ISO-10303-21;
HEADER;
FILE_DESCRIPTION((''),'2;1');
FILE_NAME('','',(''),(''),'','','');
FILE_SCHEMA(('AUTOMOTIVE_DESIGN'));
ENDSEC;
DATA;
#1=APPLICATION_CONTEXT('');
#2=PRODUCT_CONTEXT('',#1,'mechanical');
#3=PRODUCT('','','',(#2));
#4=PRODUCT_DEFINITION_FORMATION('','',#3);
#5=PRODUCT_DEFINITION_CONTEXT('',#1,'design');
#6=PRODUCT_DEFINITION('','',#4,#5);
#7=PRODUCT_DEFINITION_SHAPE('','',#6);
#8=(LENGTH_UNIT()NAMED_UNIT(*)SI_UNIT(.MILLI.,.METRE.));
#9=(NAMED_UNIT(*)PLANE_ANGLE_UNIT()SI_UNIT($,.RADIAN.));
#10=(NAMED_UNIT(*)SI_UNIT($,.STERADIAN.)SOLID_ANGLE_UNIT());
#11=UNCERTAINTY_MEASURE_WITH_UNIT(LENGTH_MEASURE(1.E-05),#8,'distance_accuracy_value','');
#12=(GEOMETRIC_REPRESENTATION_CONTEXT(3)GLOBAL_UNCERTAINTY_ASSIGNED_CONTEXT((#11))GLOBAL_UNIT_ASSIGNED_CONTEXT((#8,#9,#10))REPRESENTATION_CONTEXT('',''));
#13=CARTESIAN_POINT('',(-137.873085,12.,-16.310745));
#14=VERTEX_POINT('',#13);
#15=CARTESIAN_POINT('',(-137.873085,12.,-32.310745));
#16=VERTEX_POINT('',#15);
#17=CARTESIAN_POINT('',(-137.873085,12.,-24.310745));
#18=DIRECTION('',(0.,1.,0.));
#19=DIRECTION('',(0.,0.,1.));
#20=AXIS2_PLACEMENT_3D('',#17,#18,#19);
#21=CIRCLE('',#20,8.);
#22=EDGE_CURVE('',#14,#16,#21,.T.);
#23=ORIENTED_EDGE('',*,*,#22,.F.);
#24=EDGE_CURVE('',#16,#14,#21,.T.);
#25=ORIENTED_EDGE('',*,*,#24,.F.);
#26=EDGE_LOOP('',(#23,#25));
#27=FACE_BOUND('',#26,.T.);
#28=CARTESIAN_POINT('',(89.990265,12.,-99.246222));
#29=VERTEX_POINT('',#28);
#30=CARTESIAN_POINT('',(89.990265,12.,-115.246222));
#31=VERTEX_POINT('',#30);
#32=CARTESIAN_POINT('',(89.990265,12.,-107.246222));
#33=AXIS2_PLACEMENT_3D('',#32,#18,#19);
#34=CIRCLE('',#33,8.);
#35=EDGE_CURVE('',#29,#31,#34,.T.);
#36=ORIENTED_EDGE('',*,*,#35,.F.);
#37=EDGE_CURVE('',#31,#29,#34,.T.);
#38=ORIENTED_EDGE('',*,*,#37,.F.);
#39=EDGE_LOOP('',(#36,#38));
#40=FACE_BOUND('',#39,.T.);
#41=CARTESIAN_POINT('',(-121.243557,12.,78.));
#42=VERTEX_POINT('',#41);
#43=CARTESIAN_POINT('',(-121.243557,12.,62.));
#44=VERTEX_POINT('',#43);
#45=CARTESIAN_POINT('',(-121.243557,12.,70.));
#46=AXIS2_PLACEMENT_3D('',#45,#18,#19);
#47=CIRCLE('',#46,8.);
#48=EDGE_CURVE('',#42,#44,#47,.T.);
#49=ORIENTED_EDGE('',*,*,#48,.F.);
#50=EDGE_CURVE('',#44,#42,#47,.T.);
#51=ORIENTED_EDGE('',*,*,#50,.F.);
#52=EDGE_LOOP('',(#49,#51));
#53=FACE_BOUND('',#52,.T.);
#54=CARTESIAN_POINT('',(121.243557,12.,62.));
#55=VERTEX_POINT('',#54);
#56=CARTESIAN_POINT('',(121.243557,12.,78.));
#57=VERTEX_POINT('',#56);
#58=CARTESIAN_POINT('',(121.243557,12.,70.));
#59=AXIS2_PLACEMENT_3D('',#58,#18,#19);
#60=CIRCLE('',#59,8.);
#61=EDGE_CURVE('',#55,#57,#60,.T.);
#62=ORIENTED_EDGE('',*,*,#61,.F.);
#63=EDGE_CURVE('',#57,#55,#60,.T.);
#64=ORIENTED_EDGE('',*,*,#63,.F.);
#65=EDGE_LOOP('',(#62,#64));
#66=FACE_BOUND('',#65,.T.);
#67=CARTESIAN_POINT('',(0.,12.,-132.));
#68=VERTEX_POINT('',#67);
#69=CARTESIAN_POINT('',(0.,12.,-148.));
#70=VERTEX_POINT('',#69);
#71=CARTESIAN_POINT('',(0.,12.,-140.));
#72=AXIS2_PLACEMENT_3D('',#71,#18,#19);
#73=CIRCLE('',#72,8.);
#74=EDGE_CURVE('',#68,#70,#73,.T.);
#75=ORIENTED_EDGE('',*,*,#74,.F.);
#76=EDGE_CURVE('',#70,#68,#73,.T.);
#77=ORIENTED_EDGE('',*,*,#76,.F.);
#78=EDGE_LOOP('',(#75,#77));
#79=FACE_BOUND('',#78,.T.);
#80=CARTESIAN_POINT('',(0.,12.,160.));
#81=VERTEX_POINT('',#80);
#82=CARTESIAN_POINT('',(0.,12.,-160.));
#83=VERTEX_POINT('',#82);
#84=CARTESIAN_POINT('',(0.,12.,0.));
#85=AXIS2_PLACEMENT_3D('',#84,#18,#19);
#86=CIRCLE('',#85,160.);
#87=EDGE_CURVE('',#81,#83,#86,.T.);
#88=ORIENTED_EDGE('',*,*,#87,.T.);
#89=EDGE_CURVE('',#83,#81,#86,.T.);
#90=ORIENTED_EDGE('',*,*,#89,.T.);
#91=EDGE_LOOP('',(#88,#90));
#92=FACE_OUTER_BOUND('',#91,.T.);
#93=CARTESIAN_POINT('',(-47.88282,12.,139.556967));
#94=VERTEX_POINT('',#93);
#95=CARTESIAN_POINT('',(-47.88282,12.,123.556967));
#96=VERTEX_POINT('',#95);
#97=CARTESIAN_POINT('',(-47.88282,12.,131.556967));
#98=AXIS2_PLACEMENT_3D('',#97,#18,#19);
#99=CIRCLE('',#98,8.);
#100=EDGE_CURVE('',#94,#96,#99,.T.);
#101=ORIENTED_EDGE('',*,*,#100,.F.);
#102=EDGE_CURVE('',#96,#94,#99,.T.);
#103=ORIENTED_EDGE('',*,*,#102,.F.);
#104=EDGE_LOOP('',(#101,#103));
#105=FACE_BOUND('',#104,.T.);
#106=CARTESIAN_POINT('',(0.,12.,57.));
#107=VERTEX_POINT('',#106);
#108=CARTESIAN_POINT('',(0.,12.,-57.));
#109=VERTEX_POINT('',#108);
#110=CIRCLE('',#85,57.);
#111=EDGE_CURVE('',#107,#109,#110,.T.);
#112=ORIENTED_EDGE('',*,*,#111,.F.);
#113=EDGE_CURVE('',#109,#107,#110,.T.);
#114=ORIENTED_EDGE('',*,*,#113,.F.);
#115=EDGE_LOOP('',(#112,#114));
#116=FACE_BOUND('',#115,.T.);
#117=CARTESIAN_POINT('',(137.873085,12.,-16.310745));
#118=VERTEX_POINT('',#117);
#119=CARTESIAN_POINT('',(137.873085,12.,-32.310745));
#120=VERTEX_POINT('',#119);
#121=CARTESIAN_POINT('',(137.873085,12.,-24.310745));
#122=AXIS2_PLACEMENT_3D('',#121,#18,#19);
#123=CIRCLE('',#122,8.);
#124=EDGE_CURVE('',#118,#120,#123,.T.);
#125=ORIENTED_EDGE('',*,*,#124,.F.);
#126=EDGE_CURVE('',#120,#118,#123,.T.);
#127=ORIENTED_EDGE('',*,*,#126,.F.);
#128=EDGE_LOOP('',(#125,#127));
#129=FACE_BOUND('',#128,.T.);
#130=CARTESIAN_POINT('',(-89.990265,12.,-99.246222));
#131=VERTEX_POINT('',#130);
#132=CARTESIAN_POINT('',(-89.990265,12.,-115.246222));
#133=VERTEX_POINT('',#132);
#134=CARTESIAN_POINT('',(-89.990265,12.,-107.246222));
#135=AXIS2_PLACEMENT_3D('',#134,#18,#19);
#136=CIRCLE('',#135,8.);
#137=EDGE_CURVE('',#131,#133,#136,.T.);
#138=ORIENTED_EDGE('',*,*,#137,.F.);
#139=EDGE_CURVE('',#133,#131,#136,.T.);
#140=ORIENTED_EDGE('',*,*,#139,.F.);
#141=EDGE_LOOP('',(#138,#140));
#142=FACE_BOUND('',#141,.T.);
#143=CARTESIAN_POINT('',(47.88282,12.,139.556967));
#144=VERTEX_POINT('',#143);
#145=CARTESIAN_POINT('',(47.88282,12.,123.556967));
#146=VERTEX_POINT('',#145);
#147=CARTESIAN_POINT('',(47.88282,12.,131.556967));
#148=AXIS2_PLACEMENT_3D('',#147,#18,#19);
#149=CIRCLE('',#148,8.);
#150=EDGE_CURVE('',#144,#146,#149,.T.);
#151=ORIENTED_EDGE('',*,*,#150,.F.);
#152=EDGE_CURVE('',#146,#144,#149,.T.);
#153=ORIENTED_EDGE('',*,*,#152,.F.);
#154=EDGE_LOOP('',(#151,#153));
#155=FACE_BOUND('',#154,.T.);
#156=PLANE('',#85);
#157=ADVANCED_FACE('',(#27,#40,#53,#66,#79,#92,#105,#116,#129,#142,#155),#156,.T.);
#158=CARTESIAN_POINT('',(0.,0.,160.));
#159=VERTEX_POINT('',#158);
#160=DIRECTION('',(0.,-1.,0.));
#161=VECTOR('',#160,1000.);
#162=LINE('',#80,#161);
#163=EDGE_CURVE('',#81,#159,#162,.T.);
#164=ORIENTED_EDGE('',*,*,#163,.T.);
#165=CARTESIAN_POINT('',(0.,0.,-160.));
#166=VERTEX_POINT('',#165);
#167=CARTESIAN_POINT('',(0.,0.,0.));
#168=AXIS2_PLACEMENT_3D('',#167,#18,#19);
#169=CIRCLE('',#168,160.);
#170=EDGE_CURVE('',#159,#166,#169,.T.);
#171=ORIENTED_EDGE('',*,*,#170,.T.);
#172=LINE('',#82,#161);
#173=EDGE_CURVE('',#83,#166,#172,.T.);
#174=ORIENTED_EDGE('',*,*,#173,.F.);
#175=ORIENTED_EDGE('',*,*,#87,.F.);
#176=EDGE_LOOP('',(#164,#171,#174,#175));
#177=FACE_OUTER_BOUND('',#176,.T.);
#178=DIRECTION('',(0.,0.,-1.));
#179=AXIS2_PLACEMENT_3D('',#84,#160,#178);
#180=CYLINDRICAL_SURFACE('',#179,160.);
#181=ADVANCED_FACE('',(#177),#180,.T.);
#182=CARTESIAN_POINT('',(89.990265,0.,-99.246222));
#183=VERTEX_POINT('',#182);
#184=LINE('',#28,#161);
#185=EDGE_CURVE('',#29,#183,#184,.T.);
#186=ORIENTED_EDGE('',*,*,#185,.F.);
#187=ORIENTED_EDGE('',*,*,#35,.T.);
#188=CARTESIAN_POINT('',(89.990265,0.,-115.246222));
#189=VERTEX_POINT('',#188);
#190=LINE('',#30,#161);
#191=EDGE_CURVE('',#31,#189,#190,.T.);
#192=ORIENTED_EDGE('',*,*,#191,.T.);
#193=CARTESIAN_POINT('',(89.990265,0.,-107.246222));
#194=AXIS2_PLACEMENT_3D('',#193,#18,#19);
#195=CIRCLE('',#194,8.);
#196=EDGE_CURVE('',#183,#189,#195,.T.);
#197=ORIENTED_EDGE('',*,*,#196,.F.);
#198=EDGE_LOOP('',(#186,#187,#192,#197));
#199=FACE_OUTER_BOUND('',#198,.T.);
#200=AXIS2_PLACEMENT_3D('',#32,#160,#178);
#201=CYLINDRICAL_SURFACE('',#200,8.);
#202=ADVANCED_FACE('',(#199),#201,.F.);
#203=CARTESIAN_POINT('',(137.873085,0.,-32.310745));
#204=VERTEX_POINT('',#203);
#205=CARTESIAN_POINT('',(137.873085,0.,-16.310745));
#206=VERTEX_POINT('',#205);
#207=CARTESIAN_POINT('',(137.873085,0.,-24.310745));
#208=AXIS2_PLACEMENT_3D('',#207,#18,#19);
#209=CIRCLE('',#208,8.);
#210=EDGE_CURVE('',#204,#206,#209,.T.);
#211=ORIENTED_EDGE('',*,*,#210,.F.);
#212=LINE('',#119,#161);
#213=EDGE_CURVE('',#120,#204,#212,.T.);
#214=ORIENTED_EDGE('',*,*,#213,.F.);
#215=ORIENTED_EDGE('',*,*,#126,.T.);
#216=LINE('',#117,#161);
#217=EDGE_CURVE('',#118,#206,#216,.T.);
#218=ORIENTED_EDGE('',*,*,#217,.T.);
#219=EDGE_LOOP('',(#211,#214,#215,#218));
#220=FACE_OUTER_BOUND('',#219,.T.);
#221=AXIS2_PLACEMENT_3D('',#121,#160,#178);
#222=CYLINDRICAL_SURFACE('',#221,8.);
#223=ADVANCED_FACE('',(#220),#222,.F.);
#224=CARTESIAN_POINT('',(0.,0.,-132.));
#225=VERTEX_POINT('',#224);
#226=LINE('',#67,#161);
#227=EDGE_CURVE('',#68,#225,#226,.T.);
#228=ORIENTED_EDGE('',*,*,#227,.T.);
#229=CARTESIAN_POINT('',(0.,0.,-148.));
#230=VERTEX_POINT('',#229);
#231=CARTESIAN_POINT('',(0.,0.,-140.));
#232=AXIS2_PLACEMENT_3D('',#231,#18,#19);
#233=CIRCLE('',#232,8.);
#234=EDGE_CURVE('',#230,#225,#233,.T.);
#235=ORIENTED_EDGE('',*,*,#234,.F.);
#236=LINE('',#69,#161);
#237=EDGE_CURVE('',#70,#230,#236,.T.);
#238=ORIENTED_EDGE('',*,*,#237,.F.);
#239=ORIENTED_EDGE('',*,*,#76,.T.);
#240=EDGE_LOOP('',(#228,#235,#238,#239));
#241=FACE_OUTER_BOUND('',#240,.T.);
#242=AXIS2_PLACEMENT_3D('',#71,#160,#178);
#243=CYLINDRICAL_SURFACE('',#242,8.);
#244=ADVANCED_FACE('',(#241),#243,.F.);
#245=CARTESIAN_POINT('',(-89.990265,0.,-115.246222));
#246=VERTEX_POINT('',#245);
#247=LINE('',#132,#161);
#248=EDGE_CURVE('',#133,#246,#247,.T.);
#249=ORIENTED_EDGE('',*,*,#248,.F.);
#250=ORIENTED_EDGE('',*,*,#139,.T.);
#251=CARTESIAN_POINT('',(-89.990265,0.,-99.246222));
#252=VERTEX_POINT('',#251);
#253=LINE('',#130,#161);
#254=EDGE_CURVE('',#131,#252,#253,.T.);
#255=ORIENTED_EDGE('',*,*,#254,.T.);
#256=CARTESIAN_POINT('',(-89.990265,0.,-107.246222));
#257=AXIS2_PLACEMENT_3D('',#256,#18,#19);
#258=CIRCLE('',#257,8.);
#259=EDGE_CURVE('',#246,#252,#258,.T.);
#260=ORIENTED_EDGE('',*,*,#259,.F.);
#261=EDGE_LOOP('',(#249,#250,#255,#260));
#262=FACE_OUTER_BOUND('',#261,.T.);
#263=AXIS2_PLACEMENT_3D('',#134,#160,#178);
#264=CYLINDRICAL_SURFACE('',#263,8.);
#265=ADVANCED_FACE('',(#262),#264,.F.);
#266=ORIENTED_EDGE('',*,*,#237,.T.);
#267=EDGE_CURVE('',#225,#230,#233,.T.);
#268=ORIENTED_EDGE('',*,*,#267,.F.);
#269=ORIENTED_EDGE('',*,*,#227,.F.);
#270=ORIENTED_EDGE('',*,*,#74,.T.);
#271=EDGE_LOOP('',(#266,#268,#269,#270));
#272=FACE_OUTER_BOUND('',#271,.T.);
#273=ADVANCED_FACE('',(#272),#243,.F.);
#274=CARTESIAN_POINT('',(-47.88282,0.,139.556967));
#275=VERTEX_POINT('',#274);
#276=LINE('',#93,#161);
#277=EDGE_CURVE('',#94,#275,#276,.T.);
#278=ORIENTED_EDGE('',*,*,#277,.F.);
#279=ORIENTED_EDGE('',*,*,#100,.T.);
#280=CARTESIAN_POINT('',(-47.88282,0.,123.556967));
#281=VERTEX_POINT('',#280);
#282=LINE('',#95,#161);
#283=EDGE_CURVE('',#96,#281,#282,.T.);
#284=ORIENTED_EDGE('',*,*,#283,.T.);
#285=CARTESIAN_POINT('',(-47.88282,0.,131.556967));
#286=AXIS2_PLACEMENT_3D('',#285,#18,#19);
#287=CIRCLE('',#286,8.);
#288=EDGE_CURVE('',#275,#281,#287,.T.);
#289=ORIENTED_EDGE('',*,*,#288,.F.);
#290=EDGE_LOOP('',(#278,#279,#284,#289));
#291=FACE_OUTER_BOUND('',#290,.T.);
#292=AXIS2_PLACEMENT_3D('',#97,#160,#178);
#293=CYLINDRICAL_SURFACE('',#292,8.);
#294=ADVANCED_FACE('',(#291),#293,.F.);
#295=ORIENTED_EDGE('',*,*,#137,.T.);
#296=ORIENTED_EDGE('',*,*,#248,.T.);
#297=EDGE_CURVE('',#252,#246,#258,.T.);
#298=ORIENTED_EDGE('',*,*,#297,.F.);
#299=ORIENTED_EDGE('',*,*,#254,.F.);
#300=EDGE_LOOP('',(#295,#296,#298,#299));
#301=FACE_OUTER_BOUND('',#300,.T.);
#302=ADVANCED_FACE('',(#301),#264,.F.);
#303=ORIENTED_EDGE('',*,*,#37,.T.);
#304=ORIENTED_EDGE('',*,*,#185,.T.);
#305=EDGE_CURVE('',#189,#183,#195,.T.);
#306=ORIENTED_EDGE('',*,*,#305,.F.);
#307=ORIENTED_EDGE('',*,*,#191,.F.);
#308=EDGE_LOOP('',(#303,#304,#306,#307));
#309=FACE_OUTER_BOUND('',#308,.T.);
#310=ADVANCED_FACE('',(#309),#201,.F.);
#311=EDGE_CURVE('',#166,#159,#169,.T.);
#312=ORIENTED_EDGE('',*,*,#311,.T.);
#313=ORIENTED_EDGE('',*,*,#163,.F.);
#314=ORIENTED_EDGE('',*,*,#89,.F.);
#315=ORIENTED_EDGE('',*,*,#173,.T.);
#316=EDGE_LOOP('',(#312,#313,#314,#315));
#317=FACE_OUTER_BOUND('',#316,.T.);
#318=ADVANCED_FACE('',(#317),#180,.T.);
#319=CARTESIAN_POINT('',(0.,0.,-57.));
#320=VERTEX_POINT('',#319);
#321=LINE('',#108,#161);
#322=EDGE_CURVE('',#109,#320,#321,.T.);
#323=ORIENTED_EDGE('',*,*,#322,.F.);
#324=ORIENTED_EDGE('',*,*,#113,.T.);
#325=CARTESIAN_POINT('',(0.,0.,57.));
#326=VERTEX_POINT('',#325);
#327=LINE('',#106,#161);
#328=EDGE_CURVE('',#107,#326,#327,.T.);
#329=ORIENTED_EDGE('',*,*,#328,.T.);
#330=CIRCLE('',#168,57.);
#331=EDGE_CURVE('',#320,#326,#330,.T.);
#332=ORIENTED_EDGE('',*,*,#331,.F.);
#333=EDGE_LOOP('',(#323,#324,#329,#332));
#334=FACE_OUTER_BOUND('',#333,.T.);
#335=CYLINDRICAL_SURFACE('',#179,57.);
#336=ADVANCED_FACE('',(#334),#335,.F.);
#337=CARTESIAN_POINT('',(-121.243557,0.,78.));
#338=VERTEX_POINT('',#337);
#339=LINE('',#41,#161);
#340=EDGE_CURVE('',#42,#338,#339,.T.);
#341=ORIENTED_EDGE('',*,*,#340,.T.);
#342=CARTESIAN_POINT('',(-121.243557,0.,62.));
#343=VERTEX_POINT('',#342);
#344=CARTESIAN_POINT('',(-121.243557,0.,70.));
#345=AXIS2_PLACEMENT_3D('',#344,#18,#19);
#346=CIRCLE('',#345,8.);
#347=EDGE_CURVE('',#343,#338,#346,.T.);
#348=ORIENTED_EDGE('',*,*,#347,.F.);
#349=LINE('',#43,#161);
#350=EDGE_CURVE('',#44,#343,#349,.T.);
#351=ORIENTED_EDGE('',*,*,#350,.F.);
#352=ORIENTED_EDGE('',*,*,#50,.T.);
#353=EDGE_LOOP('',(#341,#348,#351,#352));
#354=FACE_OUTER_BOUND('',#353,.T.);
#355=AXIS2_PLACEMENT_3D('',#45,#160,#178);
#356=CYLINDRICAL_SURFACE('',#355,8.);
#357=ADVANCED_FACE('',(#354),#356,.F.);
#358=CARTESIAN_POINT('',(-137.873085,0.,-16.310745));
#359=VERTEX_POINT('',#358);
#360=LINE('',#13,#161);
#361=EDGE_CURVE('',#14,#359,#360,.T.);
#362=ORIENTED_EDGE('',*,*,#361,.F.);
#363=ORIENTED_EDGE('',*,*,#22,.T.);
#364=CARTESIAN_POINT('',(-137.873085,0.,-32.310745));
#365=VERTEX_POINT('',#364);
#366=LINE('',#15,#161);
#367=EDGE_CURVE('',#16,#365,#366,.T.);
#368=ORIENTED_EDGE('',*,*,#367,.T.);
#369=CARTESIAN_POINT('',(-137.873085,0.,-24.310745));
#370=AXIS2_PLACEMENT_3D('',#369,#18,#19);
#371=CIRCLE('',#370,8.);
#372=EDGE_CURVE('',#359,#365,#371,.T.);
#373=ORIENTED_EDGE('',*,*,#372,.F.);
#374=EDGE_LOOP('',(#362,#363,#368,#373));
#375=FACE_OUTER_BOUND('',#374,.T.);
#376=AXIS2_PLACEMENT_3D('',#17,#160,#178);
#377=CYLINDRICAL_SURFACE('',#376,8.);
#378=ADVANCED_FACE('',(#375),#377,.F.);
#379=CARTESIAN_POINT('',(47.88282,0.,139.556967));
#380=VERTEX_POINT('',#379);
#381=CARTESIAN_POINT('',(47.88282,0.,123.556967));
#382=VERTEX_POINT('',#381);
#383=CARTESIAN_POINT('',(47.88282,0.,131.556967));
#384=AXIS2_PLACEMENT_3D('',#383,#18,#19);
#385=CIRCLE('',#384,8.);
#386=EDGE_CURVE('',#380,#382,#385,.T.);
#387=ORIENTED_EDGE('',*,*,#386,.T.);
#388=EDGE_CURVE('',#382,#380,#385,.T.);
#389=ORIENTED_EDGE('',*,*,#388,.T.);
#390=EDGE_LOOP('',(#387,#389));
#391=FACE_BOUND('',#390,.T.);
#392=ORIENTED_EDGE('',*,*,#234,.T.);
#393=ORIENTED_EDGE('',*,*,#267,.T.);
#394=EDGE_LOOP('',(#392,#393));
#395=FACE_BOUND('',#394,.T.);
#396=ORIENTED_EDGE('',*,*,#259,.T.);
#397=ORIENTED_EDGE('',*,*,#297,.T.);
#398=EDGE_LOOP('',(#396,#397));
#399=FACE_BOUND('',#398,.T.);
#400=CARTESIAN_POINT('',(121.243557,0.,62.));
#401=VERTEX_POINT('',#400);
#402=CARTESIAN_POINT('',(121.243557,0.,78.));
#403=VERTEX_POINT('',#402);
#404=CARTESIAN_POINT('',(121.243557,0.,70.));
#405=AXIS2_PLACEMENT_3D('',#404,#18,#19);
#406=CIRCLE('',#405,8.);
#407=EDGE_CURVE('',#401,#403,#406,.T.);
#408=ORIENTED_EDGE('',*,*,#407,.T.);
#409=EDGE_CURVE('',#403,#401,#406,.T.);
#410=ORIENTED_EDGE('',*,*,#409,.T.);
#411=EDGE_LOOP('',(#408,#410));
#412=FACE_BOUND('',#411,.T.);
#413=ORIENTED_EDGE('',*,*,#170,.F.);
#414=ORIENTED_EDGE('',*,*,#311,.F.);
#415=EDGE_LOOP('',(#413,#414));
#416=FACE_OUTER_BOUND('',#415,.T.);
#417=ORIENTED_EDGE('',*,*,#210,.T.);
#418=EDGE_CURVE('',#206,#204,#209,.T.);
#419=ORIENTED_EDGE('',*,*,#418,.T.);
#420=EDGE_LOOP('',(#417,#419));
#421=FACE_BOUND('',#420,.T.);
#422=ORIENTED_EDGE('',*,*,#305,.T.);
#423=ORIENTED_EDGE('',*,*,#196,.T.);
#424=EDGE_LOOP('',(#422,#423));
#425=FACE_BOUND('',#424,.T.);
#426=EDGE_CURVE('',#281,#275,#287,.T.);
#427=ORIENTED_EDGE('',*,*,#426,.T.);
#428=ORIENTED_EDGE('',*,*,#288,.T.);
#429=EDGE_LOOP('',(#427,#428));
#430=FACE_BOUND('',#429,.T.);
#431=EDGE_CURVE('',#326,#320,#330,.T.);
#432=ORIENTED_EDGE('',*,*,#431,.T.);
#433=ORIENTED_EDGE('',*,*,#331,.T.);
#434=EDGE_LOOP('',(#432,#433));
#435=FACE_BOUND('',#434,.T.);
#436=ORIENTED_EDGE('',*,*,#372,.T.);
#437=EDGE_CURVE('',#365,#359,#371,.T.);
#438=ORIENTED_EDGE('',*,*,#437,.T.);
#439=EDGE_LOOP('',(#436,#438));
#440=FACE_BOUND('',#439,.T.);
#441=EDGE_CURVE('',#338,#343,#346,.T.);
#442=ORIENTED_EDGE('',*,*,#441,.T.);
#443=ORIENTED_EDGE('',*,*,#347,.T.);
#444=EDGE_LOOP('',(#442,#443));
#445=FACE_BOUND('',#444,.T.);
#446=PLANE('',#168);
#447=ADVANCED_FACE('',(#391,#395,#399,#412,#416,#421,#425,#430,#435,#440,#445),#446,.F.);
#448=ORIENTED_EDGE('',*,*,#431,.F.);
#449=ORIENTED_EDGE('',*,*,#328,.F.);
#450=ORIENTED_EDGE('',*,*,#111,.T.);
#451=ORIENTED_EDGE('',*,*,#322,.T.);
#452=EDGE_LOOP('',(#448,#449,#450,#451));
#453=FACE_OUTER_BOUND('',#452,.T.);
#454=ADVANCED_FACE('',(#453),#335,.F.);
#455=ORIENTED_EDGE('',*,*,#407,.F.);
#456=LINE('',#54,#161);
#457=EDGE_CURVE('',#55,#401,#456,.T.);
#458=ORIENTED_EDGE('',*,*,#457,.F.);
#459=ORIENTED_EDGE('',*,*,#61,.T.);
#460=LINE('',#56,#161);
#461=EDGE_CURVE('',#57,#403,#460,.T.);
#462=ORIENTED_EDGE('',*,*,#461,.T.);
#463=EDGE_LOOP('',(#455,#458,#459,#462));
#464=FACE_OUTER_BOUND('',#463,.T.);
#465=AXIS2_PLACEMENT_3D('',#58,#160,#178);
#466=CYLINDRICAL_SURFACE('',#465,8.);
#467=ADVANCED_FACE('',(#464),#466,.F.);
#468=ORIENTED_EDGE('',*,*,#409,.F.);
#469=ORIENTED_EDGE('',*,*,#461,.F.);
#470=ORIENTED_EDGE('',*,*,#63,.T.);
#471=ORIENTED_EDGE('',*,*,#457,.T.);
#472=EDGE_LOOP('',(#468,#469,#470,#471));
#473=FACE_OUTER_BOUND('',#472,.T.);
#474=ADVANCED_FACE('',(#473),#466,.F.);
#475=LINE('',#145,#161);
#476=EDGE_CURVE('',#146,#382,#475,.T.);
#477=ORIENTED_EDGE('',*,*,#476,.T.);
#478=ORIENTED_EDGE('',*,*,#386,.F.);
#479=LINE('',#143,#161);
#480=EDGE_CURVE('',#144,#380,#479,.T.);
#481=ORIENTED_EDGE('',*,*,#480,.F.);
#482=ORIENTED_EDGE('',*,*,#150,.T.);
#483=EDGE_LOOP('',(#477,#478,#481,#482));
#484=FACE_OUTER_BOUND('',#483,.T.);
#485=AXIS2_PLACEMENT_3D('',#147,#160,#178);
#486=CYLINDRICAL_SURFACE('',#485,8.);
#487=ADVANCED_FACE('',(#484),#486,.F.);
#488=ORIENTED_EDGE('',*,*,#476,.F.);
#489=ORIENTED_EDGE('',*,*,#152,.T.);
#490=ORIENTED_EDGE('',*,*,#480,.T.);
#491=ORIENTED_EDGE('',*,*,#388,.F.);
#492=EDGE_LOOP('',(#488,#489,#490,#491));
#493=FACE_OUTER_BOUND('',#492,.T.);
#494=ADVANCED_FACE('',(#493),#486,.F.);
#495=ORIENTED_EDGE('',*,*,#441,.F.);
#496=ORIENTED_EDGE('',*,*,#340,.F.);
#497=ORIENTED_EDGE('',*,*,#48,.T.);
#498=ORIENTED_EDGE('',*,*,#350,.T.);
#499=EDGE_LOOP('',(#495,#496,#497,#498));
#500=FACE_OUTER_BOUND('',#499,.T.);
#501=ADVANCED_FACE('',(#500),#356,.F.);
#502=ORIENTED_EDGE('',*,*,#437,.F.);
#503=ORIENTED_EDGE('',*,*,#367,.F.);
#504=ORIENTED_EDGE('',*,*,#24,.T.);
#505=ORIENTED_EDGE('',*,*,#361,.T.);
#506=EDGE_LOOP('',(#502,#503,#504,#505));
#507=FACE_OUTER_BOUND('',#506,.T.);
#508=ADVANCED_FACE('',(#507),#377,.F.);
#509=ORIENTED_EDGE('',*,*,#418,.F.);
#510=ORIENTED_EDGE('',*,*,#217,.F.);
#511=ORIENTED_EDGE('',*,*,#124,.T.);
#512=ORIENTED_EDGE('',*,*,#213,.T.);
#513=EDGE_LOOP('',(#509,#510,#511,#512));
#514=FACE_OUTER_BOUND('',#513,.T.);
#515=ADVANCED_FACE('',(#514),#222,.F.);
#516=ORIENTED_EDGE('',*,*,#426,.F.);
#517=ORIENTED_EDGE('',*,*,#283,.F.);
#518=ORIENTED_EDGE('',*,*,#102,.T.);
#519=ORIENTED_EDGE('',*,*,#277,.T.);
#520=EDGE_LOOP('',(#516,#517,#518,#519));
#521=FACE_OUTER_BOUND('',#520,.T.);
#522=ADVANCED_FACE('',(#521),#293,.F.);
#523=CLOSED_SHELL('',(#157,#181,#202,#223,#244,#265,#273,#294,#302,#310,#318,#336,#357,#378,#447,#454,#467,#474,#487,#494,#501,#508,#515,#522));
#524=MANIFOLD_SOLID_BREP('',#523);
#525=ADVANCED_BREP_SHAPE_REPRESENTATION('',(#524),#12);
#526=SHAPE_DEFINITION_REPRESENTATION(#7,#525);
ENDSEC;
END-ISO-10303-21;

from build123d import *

# Parameters (mm, degrees)
SKETCH1_R           = 160
SKETCH1_R_2         = 57
SKETCH1_R_3         = 8
BOSS_EXTRUDE1_DEPTH = 12


with BuildPart() as part:
    # Sketch1 → Boss-Extrude1 (new body)
    with BuildSketch(Plane(origin=(0, 0, 0), x_dir=(1, 0, 0), z_dir=(0, 1, 0))):
        with Locations(Location((0, 0, 0), (0, 0, 270))):
            Circle(SKETCH1_R)
        with Locations(Location((0, 0, 0), (0, 0, 270))):
            Circle(SKETCH1_R_2, mode=Mode.SUBTRACT)
        with Locations(Location((0, 140, 0), (0, 0, 270))):
            Circle(SKETCH1_R_3, mode=Mode.SUBTRACT)
        with Locations(Location((89.990265356, 107.246222037, 0), (0, 0, 270))):
            Circle(SKETCH1_R_3, mode=Mode.SUBTRACT)
        with Locations(Location((137.873085422, 24.310744873, 0), (0, 0, 270))):
            Circle(SKETCH1_R_3, mode=Mode.SUBTRACT)
        with Locations(Location((121.24355653, -70, 0), (0, 0, 270))):
            Circle(SKETCH1_R_3, mode=Mode.SUBTRACT)
        with Locations(Location((47.882820066, -131.55696691, 0), (0, 0, 270))):
            Circle(SKETCH1_R_3, mode=Mode.SUBTRACT)
        with Locations(Location((-47.882820066, -131.55696691, 0), (0, 0, 270))):
            Circle(SKETCH1_R_3, mode=Mode.SUBTRACT)
        with Locations(Location((-121.24355653, -70, 0), (0, 0, 270))):
            Circle(SKETCH1_R_3, mode=Mode.SUBTRACT)
        with Locations(Location((-137.873085422, 24.310744873, 0), (0, 0, 270))):
            Circle(SKETCH1_R_3, mode=Mode.SUBTRACT)
        with Locations(Location((-89.990265356, 107.246222037, 0), (0, 0, 270))):
            Circle(SKETCH1_R_3, mode=Mode.SUBTRACT)
    extrude(amount=BOSS_EXTRUDE1_DEPTH)


solid = part.part
